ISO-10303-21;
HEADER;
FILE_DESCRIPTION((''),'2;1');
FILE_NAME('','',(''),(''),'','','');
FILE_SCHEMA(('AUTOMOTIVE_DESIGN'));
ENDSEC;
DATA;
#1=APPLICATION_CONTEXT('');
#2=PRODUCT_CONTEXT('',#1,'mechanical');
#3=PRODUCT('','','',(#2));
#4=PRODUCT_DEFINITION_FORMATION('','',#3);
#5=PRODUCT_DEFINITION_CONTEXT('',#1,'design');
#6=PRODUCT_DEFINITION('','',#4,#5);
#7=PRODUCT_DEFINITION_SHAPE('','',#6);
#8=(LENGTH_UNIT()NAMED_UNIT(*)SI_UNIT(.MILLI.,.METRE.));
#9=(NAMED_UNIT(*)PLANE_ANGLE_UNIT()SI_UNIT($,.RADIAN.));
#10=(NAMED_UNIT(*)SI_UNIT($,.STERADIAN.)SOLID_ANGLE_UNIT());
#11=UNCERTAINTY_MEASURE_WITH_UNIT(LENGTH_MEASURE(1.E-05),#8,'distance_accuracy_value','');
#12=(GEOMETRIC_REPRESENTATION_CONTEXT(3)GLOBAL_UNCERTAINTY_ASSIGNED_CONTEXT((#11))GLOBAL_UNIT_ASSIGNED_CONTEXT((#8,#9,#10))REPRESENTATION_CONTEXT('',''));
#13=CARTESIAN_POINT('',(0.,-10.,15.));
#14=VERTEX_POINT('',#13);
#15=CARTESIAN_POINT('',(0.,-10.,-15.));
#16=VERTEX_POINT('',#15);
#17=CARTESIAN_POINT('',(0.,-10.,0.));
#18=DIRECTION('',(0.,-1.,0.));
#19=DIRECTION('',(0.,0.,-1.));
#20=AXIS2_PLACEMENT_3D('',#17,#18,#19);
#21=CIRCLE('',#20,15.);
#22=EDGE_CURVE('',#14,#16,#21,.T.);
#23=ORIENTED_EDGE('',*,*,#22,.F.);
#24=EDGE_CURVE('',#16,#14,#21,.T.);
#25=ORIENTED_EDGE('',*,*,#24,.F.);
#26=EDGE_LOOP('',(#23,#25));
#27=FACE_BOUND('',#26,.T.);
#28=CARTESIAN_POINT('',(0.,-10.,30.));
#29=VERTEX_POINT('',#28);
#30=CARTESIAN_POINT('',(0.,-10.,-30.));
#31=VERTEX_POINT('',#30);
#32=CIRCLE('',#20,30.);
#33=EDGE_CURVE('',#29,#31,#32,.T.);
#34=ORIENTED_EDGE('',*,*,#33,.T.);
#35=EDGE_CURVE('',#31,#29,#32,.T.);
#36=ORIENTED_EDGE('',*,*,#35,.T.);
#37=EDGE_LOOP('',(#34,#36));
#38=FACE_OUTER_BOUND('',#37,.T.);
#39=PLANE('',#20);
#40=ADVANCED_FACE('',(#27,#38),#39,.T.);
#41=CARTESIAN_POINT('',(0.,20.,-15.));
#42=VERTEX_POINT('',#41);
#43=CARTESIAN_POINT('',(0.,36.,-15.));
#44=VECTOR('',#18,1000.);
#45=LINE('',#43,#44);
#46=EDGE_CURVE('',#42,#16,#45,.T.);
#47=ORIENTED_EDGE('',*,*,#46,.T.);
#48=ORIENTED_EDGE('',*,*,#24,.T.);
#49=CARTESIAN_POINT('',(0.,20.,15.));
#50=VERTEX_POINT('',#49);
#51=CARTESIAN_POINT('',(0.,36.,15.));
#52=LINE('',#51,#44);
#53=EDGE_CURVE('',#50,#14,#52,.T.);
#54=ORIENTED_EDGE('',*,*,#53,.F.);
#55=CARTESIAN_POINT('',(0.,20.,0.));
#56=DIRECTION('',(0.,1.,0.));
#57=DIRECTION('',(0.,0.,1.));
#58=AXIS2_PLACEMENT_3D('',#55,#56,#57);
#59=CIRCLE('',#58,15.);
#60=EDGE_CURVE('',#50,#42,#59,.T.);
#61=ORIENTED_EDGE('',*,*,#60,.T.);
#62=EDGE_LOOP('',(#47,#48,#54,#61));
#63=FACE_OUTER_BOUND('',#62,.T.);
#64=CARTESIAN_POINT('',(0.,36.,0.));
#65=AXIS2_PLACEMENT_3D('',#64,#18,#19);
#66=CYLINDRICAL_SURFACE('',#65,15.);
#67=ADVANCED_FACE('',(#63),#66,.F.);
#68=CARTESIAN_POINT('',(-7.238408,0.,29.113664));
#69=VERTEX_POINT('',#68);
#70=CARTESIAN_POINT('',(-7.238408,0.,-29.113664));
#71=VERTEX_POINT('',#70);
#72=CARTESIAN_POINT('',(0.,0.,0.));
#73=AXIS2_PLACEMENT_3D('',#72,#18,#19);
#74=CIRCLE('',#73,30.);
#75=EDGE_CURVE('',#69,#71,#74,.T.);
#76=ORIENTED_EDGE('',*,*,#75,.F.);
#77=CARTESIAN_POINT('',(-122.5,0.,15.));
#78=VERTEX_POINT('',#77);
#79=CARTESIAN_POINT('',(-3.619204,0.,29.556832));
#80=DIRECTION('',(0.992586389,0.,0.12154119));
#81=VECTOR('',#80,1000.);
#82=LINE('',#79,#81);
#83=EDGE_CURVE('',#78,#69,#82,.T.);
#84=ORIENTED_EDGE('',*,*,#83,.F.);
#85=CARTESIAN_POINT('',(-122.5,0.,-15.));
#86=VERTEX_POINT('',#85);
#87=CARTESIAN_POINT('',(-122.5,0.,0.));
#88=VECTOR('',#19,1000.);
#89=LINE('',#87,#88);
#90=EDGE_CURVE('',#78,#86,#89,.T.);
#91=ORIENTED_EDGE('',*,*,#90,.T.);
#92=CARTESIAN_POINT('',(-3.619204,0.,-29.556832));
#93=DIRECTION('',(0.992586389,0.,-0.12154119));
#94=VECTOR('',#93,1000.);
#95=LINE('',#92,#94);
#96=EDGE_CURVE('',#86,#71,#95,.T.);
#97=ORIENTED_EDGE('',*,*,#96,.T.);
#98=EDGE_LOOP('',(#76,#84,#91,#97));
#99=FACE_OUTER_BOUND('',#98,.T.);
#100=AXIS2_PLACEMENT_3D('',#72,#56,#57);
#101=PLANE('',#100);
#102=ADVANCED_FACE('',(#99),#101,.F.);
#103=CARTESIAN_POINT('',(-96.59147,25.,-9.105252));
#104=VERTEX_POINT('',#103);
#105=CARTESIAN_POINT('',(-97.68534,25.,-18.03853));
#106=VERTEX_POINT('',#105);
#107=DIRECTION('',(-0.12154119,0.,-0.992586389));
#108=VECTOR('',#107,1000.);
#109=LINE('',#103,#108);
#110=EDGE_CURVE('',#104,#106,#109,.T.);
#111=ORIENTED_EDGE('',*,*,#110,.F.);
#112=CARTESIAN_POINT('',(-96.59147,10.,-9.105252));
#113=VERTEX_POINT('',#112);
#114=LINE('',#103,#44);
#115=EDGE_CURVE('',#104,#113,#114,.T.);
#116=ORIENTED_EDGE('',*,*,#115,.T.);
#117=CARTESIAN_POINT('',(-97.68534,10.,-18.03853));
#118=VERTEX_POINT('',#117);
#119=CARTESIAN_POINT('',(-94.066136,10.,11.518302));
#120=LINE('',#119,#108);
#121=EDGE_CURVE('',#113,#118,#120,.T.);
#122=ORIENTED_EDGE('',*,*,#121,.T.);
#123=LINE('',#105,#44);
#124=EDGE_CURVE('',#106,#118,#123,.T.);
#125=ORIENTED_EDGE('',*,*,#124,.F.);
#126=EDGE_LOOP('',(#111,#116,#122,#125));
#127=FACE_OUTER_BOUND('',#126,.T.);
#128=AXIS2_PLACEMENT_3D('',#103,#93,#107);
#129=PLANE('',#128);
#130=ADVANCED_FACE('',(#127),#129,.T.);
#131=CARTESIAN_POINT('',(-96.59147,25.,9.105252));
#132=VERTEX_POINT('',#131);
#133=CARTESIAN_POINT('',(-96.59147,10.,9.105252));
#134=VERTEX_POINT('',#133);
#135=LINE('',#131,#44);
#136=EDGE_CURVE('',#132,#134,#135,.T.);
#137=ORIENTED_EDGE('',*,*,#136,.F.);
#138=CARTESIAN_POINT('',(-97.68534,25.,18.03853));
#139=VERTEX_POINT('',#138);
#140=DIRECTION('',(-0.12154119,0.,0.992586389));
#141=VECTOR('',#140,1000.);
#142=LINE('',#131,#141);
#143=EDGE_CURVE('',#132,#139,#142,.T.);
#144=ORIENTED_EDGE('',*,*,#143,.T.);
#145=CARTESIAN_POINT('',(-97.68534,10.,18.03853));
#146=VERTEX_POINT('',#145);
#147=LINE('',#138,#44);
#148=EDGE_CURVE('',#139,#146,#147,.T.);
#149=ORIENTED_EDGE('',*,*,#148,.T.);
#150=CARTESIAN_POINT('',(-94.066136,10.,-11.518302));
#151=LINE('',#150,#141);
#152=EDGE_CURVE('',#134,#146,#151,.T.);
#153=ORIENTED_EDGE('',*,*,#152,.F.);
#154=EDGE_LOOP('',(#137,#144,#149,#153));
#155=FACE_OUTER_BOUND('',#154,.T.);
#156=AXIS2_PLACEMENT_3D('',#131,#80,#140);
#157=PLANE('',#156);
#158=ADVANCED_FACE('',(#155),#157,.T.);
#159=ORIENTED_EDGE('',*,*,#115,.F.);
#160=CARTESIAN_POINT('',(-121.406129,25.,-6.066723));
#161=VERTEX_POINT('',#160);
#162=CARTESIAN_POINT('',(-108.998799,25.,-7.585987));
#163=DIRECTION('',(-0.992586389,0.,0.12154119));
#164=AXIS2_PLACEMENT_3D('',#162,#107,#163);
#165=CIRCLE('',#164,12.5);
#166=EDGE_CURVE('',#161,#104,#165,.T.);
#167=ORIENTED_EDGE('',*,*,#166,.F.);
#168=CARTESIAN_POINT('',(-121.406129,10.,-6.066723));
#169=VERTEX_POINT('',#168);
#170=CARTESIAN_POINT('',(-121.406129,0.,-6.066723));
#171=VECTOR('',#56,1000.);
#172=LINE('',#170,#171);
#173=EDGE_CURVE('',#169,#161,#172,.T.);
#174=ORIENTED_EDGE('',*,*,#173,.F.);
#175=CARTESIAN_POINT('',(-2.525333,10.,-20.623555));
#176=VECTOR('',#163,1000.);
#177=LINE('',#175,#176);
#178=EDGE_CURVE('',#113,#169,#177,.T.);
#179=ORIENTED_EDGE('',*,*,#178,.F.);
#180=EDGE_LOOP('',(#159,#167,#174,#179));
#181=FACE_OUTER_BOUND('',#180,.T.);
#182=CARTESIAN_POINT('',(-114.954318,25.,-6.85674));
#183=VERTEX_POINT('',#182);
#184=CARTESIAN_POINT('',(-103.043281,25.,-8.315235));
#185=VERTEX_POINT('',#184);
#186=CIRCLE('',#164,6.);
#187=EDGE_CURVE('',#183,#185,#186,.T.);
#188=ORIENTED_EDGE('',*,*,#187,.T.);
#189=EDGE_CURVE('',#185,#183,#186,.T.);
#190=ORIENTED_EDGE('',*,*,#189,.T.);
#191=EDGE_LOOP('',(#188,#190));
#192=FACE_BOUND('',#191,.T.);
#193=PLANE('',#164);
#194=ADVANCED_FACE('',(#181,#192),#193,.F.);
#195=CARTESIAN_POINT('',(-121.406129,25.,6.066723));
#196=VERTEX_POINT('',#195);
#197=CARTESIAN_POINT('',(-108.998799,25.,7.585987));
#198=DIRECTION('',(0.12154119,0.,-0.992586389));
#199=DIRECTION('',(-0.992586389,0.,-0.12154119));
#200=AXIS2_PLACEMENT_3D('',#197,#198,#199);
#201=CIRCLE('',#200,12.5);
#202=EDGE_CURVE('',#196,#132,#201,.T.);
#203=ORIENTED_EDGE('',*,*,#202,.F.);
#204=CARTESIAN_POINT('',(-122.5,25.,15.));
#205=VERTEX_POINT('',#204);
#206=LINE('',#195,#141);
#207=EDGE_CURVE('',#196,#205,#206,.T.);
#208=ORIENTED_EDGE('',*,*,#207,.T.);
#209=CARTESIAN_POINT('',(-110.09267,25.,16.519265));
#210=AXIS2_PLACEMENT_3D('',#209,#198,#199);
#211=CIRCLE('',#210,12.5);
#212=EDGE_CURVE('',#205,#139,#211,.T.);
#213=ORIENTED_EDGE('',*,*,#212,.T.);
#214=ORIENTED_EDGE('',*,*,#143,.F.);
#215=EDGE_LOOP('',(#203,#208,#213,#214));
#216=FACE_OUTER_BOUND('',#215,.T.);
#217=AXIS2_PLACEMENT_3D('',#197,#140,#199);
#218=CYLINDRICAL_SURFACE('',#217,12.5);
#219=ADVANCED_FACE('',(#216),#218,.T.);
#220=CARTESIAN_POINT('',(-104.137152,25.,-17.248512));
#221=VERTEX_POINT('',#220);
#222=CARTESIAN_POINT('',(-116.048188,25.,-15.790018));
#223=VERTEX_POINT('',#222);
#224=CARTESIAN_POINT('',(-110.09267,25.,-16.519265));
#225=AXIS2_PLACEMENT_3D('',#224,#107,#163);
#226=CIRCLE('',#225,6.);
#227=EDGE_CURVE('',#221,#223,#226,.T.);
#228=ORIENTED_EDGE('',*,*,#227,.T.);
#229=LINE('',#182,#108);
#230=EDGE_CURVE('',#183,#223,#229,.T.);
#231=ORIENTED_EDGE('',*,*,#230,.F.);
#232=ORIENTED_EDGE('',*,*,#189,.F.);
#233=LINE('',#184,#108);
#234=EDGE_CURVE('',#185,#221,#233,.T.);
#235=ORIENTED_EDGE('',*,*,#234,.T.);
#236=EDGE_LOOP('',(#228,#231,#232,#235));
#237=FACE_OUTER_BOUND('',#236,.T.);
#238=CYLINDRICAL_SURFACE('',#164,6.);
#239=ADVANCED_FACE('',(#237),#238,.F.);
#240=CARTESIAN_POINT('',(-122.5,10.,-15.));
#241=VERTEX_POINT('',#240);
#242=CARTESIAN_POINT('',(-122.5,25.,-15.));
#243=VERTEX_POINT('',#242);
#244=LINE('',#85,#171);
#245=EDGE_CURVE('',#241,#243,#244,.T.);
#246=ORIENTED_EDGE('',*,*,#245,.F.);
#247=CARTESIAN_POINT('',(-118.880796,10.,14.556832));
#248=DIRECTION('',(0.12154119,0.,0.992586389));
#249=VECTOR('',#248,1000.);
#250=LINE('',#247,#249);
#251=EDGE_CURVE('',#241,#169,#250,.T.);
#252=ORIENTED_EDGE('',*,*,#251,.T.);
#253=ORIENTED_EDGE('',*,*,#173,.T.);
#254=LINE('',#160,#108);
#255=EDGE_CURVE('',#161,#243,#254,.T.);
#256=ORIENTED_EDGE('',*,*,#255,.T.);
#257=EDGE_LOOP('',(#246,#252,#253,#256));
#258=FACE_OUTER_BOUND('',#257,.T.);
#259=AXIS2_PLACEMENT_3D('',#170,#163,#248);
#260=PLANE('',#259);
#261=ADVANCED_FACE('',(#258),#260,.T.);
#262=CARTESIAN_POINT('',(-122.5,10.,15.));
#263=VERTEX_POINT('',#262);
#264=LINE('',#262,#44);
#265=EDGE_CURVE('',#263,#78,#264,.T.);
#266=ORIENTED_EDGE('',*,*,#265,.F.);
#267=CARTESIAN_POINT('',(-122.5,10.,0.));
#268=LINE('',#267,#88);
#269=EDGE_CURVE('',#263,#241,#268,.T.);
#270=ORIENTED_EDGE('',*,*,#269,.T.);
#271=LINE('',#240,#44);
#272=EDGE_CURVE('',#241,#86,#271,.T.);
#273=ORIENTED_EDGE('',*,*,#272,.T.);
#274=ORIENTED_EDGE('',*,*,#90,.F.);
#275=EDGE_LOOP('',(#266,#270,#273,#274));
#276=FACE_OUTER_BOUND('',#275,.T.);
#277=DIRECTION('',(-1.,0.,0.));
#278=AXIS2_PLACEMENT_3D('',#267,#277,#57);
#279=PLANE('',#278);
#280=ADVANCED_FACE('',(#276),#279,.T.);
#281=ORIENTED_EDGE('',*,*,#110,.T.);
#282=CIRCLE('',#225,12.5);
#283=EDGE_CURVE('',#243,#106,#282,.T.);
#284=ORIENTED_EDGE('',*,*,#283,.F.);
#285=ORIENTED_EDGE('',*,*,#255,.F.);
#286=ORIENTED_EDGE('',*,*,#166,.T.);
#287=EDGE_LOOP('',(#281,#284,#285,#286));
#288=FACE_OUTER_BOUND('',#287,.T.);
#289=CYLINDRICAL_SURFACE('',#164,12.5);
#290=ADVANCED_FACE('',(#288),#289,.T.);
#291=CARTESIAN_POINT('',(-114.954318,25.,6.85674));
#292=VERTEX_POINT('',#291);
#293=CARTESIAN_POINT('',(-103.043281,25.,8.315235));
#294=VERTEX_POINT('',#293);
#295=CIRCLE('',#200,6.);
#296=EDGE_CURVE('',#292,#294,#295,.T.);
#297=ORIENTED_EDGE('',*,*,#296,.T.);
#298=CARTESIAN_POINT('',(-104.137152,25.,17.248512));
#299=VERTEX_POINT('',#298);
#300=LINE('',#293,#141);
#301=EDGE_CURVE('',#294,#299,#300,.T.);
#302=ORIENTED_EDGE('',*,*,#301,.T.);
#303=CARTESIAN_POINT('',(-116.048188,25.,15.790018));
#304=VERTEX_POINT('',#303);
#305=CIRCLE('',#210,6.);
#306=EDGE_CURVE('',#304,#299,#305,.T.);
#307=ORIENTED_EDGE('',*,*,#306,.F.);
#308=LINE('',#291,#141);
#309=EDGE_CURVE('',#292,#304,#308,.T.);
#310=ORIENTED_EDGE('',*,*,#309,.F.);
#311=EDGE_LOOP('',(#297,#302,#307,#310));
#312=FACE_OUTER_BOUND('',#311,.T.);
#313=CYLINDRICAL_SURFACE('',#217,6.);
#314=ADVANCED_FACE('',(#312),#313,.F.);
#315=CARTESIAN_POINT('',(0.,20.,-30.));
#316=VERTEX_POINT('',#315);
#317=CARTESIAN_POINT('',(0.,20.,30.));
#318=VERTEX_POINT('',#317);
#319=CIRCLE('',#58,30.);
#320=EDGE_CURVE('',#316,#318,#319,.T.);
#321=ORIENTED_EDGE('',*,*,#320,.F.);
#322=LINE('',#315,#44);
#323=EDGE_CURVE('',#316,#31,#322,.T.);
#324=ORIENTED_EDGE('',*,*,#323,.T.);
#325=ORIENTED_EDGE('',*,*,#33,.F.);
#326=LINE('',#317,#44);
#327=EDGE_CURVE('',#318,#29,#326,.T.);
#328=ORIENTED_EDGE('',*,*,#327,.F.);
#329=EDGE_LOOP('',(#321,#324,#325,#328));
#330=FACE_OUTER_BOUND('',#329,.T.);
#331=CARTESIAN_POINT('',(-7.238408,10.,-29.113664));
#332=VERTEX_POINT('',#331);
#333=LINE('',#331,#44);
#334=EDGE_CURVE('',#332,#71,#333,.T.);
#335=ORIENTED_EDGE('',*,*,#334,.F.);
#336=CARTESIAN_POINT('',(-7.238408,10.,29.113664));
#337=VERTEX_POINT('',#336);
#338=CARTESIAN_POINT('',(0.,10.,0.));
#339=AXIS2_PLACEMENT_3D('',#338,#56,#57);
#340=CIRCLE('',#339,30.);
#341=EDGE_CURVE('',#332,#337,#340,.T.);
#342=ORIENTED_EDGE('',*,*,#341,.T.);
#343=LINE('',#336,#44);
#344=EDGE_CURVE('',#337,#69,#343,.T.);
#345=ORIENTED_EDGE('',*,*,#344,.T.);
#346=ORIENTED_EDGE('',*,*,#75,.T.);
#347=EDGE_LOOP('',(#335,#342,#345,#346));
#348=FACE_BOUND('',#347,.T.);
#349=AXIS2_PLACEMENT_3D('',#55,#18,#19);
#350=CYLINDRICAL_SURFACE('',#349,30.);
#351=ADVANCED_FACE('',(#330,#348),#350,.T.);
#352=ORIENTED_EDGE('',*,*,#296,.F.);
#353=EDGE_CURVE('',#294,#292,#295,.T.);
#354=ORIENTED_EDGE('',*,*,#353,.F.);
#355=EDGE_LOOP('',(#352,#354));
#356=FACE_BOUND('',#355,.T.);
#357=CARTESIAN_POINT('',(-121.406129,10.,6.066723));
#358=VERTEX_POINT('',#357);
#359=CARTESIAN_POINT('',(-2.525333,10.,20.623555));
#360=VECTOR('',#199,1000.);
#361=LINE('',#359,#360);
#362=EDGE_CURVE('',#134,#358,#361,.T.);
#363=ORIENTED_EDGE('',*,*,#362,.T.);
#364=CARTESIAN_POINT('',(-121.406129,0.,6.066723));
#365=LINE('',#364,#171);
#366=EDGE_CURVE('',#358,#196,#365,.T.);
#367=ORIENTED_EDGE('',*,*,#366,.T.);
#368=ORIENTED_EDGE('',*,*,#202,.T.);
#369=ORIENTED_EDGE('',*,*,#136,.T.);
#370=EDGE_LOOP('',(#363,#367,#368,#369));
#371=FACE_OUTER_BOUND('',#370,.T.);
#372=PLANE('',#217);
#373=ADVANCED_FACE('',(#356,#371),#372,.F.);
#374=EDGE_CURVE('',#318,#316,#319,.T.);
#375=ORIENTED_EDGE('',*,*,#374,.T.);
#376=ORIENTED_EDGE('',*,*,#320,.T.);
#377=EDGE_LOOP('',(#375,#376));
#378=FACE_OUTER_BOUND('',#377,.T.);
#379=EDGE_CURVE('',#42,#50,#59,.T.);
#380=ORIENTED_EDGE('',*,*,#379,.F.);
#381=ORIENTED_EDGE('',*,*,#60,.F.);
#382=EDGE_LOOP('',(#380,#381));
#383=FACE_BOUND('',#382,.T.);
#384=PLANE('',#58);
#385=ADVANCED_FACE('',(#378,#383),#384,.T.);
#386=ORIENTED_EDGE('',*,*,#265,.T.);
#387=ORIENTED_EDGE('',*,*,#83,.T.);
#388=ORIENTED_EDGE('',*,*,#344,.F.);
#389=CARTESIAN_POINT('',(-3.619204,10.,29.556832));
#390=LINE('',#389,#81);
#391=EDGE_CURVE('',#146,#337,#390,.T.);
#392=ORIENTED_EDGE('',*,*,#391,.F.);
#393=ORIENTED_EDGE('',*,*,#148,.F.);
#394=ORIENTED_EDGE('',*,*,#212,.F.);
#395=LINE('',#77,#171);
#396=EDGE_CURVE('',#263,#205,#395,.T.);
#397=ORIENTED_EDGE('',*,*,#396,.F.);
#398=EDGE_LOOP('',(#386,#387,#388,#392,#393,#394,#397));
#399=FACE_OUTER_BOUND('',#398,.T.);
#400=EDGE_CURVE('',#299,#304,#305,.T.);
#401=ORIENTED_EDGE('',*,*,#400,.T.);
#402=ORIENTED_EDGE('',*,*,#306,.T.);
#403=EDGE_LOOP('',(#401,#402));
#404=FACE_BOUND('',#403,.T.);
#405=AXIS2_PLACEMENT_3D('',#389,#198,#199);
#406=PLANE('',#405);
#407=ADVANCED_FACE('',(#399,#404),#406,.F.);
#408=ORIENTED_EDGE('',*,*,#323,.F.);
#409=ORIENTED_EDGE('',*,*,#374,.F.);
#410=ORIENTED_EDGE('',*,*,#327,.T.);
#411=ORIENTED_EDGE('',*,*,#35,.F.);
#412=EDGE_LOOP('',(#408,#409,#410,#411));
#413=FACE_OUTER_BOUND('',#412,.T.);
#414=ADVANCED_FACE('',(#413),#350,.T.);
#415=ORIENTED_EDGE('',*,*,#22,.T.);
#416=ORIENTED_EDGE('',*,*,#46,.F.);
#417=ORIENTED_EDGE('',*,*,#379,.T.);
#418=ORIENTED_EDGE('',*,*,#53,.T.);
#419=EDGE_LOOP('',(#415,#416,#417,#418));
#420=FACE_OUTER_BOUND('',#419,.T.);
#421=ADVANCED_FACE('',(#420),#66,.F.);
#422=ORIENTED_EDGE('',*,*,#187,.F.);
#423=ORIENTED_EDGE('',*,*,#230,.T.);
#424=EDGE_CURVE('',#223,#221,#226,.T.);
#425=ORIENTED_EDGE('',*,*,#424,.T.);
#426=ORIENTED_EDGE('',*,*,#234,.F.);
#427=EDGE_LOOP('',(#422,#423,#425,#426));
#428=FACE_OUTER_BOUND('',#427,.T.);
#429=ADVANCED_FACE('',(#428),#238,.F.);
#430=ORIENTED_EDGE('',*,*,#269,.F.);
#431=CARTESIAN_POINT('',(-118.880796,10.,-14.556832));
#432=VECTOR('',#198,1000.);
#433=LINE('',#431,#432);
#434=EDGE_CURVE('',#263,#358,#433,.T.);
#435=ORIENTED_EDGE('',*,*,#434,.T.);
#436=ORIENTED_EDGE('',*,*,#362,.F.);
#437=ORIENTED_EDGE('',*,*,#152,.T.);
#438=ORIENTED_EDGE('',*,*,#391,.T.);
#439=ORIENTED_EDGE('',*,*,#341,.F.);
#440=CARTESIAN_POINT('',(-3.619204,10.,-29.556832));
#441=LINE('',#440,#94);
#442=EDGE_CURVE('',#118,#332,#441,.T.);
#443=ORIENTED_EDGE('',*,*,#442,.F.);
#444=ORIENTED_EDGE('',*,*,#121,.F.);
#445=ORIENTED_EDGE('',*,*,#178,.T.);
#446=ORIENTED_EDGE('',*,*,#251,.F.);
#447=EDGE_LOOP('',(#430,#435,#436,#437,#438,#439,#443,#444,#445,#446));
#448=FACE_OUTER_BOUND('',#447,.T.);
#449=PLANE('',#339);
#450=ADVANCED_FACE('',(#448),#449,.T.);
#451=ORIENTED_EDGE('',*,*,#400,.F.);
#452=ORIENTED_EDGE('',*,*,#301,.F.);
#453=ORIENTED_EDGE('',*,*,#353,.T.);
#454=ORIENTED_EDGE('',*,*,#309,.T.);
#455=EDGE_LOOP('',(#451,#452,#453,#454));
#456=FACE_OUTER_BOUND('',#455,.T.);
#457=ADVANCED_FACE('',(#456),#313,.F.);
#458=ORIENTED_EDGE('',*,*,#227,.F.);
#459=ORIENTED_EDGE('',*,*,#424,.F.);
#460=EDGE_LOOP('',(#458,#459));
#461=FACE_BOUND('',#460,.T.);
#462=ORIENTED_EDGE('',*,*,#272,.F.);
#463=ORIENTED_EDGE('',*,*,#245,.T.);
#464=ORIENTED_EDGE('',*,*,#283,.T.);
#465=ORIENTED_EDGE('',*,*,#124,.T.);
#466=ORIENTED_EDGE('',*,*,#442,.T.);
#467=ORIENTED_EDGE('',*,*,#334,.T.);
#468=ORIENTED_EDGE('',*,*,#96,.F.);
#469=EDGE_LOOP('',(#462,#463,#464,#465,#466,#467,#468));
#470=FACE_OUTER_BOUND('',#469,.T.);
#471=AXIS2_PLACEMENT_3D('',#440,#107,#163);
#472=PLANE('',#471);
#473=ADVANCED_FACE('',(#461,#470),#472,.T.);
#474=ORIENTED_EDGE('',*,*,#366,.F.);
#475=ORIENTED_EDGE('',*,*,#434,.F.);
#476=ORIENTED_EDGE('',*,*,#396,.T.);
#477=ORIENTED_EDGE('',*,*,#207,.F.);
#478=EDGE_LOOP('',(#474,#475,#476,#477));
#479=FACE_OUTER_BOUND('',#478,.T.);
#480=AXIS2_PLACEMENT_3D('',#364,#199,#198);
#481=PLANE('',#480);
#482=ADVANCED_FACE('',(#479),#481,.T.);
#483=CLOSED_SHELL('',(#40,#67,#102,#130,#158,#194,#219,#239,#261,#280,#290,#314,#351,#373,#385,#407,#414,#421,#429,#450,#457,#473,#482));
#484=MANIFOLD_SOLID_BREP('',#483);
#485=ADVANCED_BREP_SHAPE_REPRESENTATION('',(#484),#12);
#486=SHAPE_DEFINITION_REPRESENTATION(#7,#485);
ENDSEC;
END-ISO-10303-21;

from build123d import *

# Parameters (mm, degrees)
HUB_PROFILE_SKETCH_R   = 30
HUB_60_DEPTH           = 20
LEVER_ARM_DEPTH        = 10
HUB_START              = 20
HUB_EXTENSION_SKETCH_R = 30
HUB_EXTENSION_DEPTH    = 20
CLEVIS_LUG_SKETCH_R    = 6
CLEVIS_LUG_DEPTH       = 9
HUB_RECESS_SKETCH_R    = 30
HUB_RECESS_CUT_DEPTH   = 10
BORE_SKETCH_R          = 15
HUB_BORE_30_DEPTH      = 46


with BuildPart() as part:
    # Hub Profile Sketch → Hub Ø60 (new body)
    with BuildSketch(Plane(origin=(0, 0, 0), x_dir=(1, 0, 0), z_dir=(0, 1, 0))):
        with Locations(Location((0, 0, 0), (0, 0, 270))):
            Circle(HUB_PROFILE_SKETCH_R)
    extrude(amount=HUB_60_DEPTH)

    # Arm Profile Sketch → Lever Arm (add)
    with BuildSketch(Plane(origin=(0, 0, 0), x_dir=(1, 0, 0), z_dir=(0, 1, 0))):
        with BuildLine():
            Line((-122.5, 0), (-30, 0))
            ThreePointArc((-30, 0), (-23.63421499, 18.477658992), (-7.238407879, 29.113664341))
            Line((-7.238407879, 29.113664341), (-122.5, 15))
            Line((-122.5, 15), (-122.5, 0))
        make_face()
        with BuildLine():
            ThreePointArc((-7.238407879, -29.113664341), (-23.63421499, -18.477658992), (-30, 0))
            Line((-30, 0), (-122.5, 0))
            Line((-122.5, 0), (-122.5, -15))
            Line((-122.5, -15), (-7.238407879, -29.113664341))
        make_face()
    extrude(amount=LEVER_ARM_DEPTH)

    # Hub Extension Sketch → Hub Extension (add)
    with BuildSketch(Plane.XZ.offset(HUB_START)):
        with Locations(Location((0, 0, 0), (0, 0, 270))):
            Circle(HUB_EXTENSION_SKETCH_R)
    extrude(amount=-HUB_EXTENSION_DEPTH)

    # Clevis Lug Sketch → Clevis Lug (add)
    with BuildSketch(Plane(origin=(-3.619203939, 0, -29.556832171), x_dir=(-0.9925863886954069, 0, 0.12154119045249893), z_dir=(-0.12154119045249893, 0, -0.9925863886954069))):
        with BuildLine():
            Line((119.768714758, 0), (119.768714758, 25))
            ThreePointArc((119.768714758, 25), (107.268714758, 37.5), (94.768714758, 25))
            Line((94.768714758, 25), (94.768714758, 0))
            Line((94.768714758, 0), (119.768714758, 0))
        make_face()
        with Locations((107.268714758, 25)):
            Circle(CLEVIS_LUG_SKETCH_R, mode=Mode.SUBTRACT)
    extrude(amount=-CLEVIS_LUG_DEPTH)

    # Clevis Lug Mirror: part across plane


with BuildPart() as part_1:
    add(part.part)
    add(part.part.mirror(Plane.XY))

    # Hub Recess Sketch → Hub Recess Cut (cut)
    with BuildSketch(Plane(origin=(0, -20, 0), x_dir=(-1, 0, 0), z_dir=(0, -1, 0))):
        with Locations(Location((0, 0, 0), (0, 0, 90))):
            Circle(HUB_RECESS_SKETCH_R)
    extrude(amount=-HUB_RECESS_CUT_DEPTH, mode=Mode.SUBTRACT)

    # Bore Sketch → Hub Bore Ø30 (cut)
    with BuildSketch(Plane(origin=(0, -10, 0), x_dir=(-1, 0, 0), z_dir=(0, -1, 0))):
        with Locations(Location((0, 0, 0), (0, 0, 90))):
            Circle(BORE_SKETCH_R)
    extrude(amount=-HUB_BORE_30_DEPTH, mode=Mode.SUBTRACT)


solid = part_1.part
